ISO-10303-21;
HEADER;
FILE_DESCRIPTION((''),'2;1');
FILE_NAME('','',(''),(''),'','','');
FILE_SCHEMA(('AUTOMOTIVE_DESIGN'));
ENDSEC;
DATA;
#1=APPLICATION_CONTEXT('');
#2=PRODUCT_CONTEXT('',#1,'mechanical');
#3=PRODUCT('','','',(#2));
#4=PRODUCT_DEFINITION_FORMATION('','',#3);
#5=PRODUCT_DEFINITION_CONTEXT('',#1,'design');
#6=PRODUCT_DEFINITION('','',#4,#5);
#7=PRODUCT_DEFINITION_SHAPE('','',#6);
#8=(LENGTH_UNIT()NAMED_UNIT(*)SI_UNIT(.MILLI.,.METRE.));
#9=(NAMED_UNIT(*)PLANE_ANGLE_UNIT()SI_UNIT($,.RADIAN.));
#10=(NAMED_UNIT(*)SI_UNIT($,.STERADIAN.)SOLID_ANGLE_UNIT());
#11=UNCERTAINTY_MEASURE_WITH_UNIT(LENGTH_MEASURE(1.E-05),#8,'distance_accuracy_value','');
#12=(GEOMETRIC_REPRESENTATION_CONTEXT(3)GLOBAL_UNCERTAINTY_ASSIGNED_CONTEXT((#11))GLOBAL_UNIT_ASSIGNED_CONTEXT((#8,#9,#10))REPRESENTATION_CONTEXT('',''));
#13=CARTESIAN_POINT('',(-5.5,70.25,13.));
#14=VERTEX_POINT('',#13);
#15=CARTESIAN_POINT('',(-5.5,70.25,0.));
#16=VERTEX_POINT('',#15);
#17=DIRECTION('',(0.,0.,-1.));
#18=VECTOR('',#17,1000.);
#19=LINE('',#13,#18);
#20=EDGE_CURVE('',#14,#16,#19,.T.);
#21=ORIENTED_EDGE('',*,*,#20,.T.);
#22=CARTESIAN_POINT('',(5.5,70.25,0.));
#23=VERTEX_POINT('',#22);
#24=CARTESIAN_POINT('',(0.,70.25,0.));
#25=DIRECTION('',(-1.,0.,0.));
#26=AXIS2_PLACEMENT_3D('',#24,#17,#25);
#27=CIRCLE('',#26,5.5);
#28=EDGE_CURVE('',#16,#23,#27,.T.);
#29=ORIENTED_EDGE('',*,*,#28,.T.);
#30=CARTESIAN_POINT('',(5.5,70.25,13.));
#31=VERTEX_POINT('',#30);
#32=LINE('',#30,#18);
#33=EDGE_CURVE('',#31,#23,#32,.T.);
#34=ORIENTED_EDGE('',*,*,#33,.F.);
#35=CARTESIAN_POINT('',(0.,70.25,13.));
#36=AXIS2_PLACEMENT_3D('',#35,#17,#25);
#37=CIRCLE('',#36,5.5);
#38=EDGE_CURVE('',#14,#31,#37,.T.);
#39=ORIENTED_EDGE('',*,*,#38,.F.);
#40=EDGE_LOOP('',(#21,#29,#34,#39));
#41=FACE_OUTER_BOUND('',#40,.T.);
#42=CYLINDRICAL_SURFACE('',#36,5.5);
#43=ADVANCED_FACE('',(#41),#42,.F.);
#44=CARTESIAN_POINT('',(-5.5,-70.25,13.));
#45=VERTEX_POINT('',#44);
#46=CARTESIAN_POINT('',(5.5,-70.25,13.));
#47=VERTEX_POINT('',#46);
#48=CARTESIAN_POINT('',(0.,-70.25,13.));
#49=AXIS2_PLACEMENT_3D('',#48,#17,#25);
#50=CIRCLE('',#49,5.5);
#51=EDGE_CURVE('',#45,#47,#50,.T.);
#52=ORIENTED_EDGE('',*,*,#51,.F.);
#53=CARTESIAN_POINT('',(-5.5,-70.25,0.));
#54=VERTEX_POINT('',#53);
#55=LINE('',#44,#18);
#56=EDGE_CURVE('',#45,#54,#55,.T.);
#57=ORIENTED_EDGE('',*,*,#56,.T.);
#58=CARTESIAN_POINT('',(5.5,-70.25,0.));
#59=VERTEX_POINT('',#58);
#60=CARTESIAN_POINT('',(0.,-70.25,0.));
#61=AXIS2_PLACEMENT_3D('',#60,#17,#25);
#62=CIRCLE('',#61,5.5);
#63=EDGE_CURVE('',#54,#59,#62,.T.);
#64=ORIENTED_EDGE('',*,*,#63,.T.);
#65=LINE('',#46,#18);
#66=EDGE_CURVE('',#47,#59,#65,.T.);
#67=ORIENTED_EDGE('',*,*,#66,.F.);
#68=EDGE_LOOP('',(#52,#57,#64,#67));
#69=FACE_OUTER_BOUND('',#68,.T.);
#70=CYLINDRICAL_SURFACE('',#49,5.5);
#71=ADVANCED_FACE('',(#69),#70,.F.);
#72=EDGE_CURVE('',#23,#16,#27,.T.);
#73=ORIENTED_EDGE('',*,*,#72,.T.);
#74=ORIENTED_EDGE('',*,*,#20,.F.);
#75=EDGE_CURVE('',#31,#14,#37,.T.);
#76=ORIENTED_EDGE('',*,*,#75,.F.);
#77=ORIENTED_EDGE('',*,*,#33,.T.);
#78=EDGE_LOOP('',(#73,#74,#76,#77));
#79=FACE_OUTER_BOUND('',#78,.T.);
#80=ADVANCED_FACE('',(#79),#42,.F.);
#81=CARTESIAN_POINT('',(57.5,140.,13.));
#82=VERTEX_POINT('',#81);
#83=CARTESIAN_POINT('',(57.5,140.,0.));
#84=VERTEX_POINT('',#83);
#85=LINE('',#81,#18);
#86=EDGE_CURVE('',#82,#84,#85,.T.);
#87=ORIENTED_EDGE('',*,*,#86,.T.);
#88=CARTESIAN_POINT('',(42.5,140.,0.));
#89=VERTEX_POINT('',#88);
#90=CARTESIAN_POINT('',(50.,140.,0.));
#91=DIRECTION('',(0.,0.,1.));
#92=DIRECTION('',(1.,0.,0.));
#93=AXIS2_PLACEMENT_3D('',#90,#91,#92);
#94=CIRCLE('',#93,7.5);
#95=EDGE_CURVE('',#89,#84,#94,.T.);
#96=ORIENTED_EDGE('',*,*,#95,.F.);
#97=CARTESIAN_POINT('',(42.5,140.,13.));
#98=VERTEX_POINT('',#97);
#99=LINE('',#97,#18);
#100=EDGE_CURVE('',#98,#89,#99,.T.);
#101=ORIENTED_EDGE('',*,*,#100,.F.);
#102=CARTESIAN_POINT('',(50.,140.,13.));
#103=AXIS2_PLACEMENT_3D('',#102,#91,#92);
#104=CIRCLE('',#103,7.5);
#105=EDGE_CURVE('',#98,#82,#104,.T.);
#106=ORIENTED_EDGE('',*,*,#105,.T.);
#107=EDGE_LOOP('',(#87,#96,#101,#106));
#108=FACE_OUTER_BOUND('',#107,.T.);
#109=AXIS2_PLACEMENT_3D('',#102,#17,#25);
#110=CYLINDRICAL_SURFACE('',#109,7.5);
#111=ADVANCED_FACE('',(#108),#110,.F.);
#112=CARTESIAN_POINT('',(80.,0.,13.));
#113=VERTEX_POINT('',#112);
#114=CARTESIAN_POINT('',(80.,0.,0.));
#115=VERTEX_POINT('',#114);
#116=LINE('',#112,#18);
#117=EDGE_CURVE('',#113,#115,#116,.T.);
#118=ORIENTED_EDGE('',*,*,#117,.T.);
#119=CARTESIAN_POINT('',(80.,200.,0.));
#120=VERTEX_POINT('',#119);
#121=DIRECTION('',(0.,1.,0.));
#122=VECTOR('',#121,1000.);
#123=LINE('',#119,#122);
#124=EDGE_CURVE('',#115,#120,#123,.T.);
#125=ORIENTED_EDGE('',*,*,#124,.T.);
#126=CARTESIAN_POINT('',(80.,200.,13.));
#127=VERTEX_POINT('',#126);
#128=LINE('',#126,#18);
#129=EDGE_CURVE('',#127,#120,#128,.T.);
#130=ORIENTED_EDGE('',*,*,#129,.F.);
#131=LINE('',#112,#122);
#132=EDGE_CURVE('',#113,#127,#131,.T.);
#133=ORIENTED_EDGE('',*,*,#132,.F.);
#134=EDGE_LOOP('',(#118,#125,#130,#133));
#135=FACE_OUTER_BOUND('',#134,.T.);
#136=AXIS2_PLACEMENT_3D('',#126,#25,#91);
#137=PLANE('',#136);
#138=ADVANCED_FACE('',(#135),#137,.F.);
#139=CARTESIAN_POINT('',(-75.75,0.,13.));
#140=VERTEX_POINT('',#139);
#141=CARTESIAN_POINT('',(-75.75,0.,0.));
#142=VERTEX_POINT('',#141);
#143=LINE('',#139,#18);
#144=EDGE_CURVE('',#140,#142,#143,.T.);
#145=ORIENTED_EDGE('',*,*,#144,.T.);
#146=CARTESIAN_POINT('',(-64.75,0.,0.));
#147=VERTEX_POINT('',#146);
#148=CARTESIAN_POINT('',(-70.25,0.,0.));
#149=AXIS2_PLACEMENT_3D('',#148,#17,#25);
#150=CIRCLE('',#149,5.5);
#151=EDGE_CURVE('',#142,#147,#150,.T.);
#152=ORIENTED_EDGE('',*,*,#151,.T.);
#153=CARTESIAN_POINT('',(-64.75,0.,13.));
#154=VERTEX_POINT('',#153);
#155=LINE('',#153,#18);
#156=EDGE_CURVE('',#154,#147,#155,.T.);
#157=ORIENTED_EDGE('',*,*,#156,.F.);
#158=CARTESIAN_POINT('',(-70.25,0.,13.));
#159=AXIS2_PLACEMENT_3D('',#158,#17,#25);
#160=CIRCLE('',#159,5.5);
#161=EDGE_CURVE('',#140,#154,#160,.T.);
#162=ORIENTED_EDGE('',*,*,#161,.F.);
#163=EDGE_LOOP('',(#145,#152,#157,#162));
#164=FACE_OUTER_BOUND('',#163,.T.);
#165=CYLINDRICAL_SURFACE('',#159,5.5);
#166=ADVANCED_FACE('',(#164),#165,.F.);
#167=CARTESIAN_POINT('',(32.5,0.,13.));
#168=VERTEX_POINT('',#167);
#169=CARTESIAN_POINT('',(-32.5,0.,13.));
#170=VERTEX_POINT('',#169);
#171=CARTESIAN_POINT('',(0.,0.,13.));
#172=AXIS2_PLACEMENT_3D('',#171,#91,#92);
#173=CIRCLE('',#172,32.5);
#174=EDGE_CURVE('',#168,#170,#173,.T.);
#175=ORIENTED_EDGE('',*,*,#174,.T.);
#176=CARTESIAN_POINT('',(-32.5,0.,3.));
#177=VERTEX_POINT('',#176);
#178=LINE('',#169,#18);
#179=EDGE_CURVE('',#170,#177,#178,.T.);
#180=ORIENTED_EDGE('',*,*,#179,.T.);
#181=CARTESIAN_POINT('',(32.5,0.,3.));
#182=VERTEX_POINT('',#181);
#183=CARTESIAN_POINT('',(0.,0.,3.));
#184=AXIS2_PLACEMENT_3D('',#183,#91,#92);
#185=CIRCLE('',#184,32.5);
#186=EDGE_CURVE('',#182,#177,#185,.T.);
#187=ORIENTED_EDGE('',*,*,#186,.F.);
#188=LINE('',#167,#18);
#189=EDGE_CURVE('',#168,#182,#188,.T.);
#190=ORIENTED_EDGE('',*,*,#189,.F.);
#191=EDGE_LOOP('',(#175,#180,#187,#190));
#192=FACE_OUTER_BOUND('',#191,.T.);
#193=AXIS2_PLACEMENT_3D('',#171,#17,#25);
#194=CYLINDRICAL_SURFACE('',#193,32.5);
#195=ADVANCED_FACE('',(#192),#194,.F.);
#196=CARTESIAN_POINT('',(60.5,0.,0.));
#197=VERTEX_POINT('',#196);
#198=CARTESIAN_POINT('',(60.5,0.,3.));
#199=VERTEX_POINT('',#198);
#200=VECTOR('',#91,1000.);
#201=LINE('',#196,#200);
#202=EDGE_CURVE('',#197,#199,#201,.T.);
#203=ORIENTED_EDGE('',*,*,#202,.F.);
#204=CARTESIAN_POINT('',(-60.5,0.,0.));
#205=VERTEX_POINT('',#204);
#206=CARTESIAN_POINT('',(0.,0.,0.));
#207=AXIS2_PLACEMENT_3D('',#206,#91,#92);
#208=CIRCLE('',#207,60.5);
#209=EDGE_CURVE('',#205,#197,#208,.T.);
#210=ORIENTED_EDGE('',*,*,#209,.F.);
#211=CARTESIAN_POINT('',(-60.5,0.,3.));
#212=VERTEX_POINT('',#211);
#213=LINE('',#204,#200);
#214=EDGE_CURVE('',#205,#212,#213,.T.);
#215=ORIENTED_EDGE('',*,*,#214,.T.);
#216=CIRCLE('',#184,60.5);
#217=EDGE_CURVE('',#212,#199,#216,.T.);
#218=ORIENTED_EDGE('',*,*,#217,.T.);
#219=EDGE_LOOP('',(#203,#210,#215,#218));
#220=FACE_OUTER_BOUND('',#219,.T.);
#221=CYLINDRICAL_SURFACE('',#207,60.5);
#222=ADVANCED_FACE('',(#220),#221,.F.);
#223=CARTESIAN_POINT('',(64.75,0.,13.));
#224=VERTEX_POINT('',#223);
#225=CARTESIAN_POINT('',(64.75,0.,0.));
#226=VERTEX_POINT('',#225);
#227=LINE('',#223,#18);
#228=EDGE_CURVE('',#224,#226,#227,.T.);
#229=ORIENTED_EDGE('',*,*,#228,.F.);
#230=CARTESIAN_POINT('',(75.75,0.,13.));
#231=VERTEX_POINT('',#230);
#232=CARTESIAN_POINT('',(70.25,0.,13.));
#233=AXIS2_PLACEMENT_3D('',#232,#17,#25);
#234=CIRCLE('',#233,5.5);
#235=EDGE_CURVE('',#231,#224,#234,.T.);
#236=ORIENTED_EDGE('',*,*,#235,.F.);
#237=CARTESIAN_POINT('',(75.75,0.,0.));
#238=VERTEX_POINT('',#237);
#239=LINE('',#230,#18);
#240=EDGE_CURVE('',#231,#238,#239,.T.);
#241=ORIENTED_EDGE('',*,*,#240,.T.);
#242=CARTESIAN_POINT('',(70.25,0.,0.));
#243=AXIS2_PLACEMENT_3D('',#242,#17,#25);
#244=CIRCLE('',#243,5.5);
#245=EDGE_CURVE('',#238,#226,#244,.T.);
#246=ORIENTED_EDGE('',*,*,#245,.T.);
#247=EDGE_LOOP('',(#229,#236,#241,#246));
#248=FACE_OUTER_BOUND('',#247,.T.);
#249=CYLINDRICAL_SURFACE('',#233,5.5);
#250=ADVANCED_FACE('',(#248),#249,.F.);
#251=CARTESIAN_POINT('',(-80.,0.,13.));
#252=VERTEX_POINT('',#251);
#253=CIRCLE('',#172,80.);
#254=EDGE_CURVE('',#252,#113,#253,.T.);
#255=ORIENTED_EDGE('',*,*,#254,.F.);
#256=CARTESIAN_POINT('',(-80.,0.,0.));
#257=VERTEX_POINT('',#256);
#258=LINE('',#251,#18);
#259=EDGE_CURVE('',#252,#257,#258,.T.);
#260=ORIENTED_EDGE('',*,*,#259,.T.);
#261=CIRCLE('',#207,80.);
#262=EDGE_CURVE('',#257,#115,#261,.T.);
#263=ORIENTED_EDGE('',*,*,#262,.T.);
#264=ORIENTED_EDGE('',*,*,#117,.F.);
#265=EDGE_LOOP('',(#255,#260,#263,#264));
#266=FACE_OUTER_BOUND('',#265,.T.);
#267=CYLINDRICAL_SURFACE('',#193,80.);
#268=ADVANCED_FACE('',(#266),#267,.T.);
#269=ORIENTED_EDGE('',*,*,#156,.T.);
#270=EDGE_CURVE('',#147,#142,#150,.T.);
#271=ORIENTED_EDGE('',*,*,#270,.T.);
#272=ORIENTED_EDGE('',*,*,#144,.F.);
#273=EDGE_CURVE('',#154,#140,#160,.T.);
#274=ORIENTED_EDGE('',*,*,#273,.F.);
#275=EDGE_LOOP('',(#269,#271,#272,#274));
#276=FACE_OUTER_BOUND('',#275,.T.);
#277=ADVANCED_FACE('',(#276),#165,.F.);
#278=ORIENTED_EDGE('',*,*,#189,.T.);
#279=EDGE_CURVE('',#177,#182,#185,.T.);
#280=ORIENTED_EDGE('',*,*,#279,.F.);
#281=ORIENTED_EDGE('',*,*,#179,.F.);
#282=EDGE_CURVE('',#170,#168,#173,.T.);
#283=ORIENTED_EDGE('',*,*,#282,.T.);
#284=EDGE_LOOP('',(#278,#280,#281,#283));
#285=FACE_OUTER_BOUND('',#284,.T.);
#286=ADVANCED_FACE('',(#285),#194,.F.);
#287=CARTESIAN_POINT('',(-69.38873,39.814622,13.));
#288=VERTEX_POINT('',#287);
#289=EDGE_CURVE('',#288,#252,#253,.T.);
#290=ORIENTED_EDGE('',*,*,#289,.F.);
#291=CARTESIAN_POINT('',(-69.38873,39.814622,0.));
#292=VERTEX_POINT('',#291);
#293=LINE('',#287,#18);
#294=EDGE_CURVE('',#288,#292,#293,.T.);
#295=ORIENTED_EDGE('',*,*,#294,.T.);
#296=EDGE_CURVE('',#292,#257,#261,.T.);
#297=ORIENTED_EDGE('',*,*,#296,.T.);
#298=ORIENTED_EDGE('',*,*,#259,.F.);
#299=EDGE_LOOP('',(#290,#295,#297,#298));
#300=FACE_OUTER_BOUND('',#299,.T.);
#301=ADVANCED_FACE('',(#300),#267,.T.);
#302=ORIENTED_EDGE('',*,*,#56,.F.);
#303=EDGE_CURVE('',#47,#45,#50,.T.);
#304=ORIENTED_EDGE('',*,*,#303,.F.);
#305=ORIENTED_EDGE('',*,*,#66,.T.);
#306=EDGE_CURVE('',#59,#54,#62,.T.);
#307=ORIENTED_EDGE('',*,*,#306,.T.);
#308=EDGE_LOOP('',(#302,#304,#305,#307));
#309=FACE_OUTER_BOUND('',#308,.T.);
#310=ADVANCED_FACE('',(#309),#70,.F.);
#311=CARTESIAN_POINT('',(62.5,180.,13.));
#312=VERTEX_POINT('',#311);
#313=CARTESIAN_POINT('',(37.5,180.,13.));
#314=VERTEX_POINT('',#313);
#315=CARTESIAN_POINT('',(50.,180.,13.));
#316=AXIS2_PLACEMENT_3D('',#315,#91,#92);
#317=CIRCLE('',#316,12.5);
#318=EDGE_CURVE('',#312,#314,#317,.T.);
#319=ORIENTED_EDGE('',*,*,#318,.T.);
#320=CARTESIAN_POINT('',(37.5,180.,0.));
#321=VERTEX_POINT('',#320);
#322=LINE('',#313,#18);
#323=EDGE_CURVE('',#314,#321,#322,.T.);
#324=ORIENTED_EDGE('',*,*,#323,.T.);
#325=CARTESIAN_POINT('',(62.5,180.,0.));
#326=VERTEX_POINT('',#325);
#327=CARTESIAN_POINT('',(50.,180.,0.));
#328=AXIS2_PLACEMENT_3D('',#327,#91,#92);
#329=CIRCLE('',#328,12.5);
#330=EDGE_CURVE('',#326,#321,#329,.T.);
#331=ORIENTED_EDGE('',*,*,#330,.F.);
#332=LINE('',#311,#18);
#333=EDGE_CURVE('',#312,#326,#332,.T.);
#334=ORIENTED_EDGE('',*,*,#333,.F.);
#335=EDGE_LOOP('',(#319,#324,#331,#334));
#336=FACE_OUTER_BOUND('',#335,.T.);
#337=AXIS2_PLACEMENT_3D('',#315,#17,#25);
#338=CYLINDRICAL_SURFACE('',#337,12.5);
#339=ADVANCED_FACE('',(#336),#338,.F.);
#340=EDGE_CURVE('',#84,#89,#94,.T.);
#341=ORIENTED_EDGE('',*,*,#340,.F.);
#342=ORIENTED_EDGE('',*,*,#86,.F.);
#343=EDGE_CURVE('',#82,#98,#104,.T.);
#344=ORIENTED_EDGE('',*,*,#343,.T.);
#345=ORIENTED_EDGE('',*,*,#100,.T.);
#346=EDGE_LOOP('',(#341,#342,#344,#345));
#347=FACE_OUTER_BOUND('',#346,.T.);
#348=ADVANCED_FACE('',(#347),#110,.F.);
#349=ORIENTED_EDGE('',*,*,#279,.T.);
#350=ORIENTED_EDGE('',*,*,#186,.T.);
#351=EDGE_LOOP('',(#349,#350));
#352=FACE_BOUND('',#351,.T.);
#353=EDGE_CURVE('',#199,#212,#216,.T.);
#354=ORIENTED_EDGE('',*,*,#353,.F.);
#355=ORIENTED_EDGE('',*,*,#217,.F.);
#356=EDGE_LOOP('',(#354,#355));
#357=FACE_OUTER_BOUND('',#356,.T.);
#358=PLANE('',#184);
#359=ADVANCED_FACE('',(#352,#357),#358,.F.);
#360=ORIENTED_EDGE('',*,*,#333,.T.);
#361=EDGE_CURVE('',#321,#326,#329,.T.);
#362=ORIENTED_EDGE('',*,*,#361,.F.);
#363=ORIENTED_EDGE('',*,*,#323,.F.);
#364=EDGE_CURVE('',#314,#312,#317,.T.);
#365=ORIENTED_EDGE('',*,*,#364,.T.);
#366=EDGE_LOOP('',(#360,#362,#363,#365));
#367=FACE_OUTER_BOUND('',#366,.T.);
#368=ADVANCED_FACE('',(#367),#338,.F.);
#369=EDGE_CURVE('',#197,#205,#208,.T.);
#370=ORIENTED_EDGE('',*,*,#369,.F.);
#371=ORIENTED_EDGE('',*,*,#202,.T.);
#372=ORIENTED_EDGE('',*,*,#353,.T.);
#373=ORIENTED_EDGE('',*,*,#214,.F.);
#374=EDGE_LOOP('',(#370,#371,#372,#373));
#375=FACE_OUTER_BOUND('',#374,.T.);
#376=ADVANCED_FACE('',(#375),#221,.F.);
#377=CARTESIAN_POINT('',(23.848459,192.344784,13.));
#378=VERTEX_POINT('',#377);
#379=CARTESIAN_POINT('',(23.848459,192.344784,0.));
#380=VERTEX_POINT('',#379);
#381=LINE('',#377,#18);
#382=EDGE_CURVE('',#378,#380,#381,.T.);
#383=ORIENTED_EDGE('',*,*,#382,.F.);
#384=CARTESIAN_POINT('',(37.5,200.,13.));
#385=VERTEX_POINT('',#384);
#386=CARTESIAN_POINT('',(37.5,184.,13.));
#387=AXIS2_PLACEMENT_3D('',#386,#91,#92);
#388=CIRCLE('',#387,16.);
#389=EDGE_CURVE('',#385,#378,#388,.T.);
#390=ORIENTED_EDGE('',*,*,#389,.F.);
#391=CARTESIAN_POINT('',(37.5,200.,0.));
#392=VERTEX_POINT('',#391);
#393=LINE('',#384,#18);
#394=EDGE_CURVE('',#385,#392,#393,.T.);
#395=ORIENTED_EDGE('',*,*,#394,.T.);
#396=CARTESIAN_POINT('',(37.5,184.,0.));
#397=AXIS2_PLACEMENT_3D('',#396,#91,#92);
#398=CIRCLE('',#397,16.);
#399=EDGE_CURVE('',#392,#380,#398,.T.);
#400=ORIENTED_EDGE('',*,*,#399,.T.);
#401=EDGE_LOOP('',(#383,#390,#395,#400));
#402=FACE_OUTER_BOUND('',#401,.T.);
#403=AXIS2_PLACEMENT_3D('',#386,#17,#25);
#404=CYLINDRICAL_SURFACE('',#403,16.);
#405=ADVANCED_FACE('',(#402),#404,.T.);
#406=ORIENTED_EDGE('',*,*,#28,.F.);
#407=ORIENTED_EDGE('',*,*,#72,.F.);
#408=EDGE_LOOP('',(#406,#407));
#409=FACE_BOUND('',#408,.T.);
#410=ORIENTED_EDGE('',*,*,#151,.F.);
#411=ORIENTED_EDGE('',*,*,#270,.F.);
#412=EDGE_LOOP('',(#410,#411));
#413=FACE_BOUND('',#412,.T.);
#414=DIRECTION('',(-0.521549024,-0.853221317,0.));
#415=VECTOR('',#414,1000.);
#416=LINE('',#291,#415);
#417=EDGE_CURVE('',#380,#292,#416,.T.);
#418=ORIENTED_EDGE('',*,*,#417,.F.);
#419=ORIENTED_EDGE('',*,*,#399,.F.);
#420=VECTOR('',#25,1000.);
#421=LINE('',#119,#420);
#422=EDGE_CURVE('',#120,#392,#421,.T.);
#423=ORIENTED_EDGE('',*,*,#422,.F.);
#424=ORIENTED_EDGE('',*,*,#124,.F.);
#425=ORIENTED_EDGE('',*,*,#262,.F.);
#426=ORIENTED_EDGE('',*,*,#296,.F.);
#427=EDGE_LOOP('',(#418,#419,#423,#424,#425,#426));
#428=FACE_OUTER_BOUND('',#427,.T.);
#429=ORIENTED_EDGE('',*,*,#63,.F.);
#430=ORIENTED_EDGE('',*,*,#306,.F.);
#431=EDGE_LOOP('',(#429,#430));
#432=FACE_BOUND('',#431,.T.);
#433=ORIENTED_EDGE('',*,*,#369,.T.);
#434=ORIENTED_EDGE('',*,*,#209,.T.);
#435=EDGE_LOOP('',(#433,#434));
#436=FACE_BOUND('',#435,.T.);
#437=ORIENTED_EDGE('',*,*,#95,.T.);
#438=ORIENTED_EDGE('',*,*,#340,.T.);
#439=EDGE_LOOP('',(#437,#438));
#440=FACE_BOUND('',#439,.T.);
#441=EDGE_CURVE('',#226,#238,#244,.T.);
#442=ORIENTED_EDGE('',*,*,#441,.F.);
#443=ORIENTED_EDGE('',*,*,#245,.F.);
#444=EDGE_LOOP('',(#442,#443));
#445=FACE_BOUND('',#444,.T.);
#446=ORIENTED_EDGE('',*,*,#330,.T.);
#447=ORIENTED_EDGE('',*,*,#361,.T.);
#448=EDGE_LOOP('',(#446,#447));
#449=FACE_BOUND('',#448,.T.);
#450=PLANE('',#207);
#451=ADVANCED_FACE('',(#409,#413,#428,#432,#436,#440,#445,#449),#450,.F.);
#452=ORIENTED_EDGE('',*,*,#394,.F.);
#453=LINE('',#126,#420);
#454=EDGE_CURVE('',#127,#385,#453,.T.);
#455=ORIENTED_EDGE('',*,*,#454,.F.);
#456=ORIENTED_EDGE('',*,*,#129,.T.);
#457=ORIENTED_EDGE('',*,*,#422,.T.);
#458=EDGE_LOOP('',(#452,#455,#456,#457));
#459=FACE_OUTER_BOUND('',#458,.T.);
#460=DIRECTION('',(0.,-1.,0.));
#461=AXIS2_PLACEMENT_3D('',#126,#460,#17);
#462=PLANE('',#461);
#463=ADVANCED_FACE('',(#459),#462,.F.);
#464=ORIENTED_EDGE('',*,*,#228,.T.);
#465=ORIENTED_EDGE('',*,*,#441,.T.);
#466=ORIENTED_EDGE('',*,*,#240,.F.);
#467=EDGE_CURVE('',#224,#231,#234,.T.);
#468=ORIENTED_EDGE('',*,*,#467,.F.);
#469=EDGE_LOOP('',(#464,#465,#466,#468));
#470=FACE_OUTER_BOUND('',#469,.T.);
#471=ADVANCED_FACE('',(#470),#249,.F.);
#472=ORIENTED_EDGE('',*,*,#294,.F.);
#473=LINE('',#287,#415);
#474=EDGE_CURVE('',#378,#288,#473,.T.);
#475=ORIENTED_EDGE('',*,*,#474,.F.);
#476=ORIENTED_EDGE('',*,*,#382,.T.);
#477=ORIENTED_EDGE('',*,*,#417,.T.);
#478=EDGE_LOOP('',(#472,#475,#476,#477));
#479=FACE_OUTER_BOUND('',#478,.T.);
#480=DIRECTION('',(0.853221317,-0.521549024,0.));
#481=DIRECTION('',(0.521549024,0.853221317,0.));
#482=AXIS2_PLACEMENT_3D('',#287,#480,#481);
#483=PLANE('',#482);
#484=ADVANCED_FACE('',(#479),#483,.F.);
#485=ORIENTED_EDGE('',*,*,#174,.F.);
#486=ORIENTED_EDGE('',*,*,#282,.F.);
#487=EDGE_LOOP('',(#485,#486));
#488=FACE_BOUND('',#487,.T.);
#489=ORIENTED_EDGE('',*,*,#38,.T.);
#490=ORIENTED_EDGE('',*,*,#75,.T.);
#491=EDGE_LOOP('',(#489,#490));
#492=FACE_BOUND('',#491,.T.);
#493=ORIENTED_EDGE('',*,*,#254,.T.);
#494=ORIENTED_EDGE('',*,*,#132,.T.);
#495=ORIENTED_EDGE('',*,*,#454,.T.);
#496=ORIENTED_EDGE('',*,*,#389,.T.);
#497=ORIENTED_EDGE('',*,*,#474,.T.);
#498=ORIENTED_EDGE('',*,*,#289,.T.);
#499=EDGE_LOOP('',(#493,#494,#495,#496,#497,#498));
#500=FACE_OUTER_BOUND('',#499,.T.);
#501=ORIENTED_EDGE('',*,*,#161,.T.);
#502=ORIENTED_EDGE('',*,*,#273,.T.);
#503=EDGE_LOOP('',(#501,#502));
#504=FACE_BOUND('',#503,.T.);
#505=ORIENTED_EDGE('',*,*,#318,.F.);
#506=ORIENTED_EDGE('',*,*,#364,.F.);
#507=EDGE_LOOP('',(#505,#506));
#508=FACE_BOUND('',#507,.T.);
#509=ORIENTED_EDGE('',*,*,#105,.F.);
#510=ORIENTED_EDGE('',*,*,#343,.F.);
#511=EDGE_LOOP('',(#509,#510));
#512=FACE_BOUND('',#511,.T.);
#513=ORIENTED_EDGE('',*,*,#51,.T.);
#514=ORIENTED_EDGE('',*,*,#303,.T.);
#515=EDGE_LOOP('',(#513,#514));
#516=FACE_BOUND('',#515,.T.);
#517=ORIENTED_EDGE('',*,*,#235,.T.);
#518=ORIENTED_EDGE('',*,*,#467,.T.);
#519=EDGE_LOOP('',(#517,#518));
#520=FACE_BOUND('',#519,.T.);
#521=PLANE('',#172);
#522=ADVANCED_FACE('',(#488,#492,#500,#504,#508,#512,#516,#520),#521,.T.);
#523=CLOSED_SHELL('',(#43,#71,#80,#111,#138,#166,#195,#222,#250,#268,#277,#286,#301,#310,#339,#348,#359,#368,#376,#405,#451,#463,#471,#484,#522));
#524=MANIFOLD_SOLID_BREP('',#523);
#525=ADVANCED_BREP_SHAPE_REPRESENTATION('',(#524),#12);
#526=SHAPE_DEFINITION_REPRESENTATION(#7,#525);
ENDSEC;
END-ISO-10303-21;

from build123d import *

# Parameters (mm, degrees)
SKETCH_1_R          = 32.5
SKETCH_1_R_2        = 12.5
SKETCH_1_R_3        = 7.5
EXTRUDE_1_DEPTH     = 13
CUT_EXTRUDE_START   = 3
SKETCH_2_R          = 60.5
CUT_EXTRUDE_2_DEPTH = 219.79851714
SKETCH_4_R          = 5.5
CUT_EXTRUDE_3_DEPTH = 216.79851714


with BuildPart() as part:
    # 草图1 → 凸台-拉伸1 (new body)
    with BuildSketch(Plane.XY):
        with BuildLine():
            Line((80, 200), (37.5, 200))
            ThreePointArc((37.5, 200), (29.674290769, 197.955582218), (23.848458927, 192.34478438))
            Line((23.848458927, 192.34478438), (-69.388730207, 39.814621941))
            ThreePointArc((-69.388730207, 39.814621941), (-20.602203565, -77.30167662), (80, 0))
            Line((80, 0), (80, 160))
            Line((80, 160), (80, 200))
        make_face()
        with Locations(Location((0, 0, 0), (0, 0, 180))):
            Circle(SKETCH_1_R, mode=Mode.SUBTRACT)
        with Locations(Location((50, 180, 0), (0, 0, 180))):
            Circle(SKETCH_1_R_2, mode=Mode.SUBTRACT)
        with Locations(Location((50, 140, 0), (0, 0, 180))):
            Circle(SKETCH_1_R_3, mode=Mode.SUBTRACT)
    extrude(amount=EXTRUDE_1_DEPTH)

    # 草图2 → 切除-拉伸2 (cut, through all)
    with BuildSketch(Plane.XY.offset(CUT_EXTRUDE_START)):
        Circle(SKETCH_2_R)
    extrude(amount=-CUT_EXTRUDE_2_DEPTH, mode=Mode.SUBTRACT)

    # 草图4 → 切除-拉伸3 (cut, through all)
    with BuildSketch(Plane(origin=(0, 0, 0), x_dir=(-1, 0, 0), z_dir=(0, 0, -1))):
        with Locations((70.25, 0)):
            Circle(SKETCH_4_R)
        with Locations((0, -70.25)):
            Circle(SKETCH_4_R)
        with Locations((-70.25, 0)):
            Circle(SKETCH_4_R)
        with Locations((0, 70.25)):
            Circle(SKETCH_4_R)
    extrude(amount=-CUT_EXTRUDE_3_DEPTH, mode=Mode.SUBTRACT)


solid = part.part
